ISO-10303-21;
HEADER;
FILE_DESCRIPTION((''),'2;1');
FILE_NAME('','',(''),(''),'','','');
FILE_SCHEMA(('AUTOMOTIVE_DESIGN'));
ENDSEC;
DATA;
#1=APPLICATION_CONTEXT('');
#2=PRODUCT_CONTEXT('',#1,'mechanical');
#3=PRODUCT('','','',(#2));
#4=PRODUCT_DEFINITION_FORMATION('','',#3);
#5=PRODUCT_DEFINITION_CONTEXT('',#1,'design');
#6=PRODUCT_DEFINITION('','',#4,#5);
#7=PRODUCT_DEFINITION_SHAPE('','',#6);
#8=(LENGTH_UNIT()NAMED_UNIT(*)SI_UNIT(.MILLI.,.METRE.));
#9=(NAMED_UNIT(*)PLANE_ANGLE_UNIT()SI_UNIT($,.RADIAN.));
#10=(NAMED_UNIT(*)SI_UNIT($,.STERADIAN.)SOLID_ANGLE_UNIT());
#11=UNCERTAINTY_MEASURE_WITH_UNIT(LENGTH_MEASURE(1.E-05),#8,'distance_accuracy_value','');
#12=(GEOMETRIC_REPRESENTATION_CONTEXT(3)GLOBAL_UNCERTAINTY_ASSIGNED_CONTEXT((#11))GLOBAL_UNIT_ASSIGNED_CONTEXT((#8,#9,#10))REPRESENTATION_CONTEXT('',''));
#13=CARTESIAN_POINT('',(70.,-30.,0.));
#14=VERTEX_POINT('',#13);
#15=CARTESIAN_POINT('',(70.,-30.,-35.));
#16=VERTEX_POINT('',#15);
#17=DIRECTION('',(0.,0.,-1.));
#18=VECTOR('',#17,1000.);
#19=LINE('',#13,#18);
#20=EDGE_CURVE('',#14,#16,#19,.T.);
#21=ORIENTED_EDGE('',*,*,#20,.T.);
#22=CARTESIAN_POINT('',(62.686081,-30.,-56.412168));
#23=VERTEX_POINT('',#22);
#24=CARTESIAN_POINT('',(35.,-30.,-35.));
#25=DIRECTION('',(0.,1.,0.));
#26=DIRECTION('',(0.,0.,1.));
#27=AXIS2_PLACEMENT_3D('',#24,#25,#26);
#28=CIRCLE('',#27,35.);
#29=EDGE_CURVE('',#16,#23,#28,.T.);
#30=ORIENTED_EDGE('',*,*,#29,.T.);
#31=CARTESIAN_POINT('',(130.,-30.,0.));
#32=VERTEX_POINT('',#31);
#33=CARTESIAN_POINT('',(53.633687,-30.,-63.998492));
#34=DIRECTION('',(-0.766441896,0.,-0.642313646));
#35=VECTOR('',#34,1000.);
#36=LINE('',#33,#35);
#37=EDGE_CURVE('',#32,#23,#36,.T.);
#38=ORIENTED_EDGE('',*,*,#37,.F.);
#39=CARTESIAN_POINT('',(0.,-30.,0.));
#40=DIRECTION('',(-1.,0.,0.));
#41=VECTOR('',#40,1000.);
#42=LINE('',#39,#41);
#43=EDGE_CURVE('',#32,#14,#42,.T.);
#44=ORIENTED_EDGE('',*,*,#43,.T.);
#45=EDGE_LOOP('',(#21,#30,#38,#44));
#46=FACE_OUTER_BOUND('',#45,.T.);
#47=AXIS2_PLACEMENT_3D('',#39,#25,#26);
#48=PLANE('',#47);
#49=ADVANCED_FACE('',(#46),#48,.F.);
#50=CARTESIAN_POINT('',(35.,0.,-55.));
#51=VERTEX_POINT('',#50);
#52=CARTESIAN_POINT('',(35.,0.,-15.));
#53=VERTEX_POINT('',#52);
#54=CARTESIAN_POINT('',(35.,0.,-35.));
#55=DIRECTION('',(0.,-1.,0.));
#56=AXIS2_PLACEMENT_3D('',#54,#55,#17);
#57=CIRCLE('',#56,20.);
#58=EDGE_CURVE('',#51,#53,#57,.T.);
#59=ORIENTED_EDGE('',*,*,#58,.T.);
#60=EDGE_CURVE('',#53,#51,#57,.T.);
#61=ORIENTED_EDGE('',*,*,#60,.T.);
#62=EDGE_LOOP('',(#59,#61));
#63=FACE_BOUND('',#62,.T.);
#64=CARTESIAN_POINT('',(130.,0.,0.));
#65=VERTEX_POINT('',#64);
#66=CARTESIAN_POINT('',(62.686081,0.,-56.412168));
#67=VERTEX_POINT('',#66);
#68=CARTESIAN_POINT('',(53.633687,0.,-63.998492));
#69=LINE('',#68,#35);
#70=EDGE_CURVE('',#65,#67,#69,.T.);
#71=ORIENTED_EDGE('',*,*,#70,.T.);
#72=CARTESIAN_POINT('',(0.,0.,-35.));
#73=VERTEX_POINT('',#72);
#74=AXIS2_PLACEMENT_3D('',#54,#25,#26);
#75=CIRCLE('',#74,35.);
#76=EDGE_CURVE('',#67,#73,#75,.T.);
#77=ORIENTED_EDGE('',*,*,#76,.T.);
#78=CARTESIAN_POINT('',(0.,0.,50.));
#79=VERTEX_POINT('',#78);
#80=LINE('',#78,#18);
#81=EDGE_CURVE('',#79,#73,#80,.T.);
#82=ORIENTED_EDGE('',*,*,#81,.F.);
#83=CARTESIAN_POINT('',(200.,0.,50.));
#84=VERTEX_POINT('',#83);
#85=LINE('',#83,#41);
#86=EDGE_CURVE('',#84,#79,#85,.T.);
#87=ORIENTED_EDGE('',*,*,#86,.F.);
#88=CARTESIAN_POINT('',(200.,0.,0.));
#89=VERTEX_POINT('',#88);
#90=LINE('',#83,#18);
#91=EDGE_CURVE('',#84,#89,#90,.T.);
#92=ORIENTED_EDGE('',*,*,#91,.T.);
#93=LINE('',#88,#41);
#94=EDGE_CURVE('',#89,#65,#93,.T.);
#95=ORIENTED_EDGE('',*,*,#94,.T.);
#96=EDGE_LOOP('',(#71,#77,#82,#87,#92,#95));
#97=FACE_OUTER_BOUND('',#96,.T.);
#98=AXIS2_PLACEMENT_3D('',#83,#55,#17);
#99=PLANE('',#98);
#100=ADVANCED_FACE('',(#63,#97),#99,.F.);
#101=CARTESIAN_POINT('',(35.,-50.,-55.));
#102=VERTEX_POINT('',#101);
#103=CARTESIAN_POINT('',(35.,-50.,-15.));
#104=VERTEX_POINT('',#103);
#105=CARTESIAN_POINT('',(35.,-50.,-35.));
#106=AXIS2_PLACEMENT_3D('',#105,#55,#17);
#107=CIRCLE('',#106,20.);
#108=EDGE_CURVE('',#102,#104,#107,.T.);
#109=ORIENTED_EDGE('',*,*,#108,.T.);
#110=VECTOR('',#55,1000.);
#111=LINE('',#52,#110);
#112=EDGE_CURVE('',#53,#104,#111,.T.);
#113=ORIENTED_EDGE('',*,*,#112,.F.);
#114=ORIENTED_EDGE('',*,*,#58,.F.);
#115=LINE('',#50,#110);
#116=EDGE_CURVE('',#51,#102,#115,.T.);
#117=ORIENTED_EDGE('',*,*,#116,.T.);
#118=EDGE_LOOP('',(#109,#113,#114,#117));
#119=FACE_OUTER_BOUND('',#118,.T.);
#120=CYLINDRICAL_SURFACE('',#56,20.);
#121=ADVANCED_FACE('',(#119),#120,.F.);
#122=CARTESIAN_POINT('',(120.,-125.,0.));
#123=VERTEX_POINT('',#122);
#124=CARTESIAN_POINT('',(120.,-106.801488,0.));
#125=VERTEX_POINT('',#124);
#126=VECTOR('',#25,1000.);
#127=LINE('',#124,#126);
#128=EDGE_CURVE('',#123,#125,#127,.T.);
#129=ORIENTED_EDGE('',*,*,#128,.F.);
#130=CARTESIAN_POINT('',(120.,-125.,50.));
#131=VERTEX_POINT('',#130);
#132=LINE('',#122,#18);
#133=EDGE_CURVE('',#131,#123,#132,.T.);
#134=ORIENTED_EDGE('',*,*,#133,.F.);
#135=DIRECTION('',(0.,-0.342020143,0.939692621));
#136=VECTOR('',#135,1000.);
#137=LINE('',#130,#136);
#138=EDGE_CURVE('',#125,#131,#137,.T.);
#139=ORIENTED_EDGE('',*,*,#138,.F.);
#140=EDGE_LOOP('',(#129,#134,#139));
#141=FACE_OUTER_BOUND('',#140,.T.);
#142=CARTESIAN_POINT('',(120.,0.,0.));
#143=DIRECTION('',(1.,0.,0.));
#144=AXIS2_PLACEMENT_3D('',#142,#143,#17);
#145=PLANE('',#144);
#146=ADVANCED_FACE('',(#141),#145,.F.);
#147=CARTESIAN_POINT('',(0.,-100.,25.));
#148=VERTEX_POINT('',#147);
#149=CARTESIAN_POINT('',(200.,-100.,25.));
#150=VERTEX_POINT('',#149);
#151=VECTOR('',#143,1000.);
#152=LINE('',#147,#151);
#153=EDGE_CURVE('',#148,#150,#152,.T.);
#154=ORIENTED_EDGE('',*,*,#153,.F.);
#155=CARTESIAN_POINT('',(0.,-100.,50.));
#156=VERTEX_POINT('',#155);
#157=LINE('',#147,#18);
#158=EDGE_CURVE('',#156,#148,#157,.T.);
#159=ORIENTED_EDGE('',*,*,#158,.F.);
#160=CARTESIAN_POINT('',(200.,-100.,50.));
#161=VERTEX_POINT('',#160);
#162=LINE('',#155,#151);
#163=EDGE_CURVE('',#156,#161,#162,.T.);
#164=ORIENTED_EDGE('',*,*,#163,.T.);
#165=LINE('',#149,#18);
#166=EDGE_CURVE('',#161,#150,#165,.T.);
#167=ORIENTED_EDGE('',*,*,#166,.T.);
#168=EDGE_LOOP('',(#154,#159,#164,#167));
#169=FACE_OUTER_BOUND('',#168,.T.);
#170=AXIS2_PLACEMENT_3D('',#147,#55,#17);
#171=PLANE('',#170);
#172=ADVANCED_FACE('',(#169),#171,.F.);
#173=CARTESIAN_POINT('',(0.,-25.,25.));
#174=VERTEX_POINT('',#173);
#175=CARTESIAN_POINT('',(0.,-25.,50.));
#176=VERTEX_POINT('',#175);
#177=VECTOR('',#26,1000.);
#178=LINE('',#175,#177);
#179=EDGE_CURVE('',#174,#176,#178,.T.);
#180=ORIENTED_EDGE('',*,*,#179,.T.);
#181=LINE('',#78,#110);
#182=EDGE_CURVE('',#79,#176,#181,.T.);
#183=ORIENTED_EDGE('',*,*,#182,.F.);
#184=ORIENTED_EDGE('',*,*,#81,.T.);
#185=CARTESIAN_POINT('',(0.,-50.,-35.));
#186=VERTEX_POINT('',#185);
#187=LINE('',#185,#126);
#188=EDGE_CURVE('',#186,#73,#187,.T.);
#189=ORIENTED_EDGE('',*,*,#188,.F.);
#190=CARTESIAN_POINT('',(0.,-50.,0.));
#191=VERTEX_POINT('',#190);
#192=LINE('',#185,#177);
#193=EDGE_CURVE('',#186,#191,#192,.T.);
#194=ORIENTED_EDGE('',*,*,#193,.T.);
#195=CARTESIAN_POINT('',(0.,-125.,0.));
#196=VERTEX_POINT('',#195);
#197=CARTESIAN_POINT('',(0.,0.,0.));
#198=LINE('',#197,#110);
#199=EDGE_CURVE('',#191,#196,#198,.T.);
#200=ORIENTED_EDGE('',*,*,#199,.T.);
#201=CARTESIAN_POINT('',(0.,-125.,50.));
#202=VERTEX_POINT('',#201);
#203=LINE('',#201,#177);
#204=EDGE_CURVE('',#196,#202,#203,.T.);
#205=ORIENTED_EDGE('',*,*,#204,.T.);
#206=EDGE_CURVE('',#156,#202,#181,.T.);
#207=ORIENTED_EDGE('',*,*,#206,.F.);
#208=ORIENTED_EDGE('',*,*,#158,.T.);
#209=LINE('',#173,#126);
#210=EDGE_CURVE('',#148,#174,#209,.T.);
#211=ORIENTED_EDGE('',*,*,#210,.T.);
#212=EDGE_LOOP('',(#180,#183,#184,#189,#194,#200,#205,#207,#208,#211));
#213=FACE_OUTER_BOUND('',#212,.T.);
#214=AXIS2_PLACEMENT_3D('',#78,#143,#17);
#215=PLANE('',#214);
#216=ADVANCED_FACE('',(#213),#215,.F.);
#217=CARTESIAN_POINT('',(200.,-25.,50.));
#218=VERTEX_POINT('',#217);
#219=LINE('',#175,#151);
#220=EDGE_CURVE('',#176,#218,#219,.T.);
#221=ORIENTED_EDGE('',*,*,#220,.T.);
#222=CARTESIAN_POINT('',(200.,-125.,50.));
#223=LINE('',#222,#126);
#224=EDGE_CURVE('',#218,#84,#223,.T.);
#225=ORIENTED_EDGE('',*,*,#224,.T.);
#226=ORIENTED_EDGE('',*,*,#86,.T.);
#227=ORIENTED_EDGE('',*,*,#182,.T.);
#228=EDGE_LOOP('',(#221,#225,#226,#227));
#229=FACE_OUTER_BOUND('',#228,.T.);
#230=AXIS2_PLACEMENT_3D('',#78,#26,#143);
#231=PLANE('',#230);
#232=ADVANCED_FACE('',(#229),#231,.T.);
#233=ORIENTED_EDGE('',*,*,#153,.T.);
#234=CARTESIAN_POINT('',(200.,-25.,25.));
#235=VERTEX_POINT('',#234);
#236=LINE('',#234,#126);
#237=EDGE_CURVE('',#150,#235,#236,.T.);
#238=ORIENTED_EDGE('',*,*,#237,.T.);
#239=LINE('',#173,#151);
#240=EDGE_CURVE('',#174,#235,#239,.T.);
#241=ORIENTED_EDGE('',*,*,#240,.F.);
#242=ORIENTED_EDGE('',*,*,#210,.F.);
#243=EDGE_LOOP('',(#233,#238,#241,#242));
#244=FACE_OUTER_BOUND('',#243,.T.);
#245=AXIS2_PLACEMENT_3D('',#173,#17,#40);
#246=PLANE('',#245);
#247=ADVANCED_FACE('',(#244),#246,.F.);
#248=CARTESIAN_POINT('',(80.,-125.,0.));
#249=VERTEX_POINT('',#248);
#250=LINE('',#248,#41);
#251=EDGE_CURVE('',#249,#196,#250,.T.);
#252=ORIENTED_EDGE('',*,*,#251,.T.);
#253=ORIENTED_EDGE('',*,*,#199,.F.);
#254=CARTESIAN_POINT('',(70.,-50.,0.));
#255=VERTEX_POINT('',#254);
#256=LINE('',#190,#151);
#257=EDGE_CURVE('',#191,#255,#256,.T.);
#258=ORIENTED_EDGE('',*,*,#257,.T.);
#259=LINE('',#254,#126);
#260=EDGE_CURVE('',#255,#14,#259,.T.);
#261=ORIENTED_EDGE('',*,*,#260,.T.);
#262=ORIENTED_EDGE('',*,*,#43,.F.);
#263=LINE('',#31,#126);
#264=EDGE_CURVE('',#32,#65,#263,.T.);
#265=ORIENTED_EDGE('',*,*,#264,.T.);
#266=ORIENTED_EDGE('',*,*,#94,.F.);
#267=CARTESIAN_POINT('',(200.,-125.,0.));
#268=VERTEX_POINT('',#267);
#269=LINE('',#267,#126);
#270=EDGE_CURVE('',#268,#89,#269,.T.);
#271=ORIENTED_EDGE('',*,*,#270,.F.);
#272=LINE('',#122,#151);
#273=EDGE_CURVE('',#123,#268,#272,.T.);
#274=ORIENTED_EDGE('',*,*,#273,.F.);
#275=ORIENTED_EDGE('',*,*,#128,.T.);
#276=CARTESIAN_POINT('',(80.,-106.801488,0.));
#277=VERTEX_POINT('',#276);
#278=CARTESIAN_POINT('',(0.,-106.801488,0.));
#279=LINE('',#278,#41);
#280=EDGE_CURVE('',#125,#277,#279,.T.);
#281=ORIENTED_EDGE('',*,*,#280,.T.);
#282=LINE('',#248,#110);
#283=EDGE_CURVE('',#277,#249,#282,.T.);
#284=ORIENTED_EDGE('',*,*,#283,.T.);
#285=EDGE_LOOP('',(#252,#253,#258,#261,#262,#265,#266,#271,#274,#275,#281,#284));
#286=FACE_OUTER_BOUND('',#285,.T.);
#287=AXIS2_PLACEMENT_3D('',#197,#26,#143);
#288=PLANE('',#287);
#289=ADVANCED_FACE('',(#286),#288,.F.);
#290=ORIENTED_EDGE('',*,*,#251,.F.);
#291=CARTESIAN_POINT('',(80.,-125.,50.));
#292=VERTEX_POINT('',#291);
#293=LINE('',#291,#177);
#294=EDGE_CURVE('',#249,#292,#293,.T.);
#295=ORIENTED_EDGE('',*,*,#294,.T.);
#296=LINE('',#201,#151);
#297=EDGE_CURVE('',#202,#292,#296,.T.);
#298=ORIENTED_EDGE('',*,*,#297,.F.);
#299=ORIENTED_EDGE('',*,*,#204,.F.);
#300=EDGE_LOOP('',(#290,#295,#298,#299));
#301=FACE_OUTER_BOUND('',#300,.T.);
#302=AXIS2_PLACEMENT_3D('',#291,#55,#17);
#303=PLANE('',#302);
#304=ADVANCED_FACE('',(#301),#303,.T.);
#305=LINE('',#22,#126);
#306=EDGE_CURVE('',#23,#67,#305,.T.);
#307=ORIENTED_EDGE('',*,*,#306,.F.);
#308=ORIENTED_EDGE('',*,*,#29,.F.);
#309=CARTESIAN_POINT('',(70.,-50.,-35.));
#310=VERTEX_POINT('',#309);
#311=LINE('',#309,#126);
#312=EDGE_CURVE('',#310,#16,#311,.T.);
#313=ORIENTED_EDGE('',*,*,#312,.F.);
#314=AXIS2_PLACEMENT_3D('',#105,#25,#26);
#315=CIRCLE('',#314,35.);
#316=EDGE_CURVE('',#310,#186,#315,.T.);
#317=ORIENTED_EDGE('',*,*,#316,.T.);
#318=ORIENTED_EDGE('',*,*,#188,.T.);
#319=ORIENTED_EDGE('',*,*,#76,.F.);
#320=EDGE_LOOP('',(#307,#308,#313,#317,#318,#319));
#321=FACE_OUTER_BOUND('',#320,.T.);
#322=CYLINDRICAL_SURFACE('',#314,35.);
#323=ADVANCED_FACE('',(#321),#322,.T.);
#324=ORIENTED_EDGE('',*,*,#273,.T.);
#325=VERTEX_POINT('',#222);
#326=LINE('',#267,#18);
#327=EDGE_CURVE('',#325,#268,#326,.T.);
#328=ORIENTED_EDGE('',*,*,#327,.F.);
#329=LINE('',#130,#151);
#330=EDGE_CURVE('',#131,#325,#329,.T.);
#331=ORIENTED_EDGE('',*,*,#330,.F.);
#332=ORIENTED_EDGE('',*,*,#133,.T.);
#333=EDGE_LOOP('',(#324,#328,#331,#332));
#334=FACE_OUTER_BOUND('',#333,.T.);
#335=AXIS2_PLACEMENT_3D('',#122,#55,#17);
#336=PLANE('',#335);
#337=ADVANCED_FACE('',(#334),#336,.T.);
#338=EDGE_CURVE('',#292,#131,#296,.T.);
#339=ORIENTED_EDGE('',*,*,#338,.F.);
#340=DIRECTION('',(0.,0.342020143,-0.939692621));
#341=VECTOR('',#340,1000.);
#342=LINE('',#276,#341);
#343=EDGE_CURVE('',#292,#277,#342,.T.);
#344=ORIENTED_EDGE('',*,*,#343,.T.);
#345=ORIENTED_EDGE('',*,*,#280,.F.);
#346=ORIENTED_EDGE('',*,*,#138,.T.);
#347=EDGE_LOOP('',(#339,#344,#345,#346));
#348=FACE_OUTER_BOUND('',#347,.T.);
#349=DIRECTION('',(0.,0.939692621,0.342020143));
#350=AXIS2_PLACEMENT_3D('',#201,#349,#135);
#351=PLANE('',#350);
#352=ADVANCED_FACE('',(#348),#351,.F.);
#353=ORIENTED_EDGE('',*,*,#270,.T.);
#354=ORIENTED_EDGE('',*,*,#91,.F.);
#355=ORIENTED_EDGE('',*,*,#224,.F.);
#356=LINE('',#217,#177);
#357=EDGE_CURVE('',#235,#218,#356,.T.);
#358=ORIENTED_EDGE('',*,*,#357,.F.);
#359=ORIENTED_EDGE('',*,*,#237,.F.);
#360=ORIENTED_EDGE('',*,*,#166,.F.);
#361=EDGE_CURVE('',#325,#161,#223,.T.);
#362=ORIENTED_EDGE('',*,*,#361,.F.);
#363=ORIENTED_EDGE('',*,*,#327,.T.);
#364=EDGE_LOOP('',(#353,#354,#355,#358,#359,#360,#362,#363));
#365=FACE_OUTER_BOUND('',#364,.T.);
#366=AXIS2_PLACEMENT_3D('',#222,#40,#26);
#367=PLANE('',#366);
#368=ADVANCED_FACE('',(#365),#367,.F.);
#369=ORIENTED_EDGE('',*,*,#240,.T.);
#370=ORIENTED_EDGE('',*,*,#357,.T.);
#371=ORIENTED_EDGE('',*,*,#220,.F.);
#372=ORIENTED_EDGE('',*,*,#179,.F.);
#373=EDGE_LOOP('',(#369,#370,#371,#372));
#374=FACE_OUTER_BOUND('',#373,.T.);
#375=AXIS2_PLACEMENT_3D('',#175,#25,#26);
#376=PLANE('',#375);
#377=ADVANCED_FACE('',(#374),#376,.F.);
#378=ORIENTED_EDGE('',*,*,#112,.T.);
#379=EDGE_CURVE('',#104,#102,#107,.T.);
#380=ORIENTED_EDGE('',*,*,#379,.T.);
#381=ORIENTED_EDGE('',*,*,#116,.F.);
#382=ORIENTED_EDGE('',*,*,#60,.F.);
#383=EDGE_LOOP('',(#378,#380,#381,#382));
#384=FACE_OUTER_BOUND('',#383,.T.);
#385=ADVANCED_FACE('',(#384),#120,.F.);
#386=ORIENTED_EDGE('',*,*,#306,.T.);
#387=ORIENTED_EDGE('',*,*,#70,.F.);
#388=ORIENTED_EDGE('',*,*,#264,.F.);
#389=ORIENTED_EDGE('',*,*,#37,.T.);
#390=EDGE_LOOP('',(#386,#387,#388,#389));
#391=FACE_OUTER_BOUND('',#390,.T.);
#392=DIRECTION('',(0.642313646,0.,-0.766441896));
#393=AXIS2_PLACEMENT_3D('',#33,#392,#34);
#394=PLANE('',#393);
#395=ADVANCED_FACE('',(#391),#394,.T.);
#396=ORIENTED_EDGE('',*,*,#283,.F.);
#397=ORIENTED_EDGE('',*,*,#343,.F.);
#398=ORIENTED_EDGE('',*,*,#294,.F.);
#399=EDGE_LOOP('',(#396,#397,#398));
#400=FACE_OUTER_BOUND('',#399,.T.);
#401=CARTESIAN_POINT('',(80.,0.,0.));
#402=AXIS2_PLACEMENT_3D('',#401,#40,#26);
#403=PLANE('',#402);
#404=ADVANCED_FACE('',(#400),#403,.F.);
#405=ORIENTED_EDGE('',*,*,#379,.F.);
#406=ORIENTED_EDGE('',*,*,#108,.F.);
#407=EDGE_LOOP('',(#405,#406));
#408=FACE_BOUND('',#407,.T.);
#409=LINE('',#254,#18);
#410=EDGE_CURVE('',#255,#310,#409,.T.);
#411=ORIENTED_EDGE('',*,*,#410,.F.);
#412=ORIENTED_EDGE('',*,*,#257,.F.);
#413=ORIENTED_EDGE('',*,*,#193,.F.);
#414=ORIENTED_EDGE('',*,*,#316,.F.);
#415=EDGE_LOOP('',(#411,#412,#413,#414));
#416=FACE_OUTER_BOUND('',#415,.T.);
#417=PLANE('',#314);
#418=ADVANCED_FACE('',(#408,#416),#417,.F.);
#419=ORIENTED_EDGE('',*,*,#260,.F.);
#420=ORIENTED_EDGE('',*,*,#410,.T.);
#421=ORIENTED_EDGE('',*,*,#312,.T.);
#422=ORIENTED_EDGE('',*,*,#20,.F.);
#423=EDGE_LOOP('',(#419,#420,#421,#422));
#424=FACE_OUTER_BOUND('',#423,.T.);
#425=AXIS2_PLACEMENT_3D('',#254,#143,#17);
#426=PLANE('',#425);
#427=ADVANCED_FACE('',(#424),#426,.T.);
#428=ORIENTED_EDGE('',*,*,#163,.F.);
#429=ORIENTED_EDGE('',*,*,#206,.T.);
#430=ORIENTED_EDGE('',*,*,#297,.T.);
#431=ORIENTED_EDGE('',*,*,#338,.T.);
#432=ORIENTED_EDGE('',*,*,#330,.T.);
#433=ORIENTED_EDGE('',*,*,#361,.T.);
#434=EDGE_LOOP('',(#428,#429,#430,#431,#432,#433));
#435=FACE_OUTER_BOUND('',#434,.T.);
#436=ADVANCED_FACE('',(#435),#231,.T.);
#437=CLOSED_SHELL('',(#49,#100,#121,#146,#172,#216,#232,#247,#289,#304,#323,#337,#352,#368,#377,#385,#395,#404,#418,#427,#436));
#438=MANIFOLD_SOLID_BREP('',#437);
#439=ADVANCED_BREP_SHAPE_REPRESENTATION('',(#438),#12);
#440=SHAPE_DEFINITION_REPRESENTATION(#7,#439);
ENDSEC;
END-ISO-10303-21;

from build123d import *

# Parameters (mm, degrees)
BASE_BLOCK_SKETCH_W   = 200
BASE_BLOCK_SKETCH_H   = 125
BASE_BLOCK_DEPTH      = 50
UPPER_BLOCK_DEPTH     = 50
LUG_BOSS_DEPTH        = 30
LUG_BORE_SKETCH_R     = 20
LUG_BORE_DEPTH        = 50
CHANNEL_CUT_DEPTH     = 200
CORNER_TRIM_CUT_DEPTH = 200
TAPER_FILL_1_DEPTH    = 80
TAPER_FILL_2_DEPTH    = 80


with BuildPart() as part:
    # Base Block Sketch → Base Block (new body)
    with BuildSketch(Plane.XY):
        with Locations((100, -62.5)):
            Rectangle(BASE_BLOCK_SKETCH_W, BASE_BLOCK_SKETCH_H)
    extrude(amount=BASE_BLOCK_DEPTH)

    # Upper Block Sketch → Upper Block (add)
    with BuildSketch(Plane(origin=(0, 0, 0), x_dir=(1, 0, 0), z_dir=(0, 1, 0))):
        with BuildLine():
            Line((0, 0), (70, 0))
            Line((70, 0), (70, 35))
            ThreePointArc((70, 35), (35, 70), (0, 35))
            Line((0, 35), (0, 0))
        make_face()
    extrude(amount=-UPPER_BLOCK_DEPTH)

    # Lug Sketch → Lug Boss (add)
    with BuildSketch(Plane(origin=(0, 0, 0), x_dir=(1, 0, 0), z_dir=(0, 1, 0))):
        with BuildLine():
            Line((70, 0), (130, 0))
            Line((130, 0), (62.686080753, 56.412167861))
            ThreePointArc((62.686080753, 56.412167861), (68.121087138, 46.31342507), (70, 35))
            Line((70, 35), (70, 0))
        make_face()
    extrude(amount=-LUG_BOSS_DEPTH)

    # Lug Bore Sketch → Lug Bore (cut)
    with BuildSketch(Plane.XZ.offset(50)):
        with Locations(Location((35, -35, 0), (0, 0, 270))):
            Circle(LUG_BORE_SKETCH_R)
    extrude(amount=-LUG_BORE_DEPTH, mode=Mode.SUBTRACT)

    # Channel Sketch → Channel Cut (cut)
    with BuildSketch(Plane(origin=(200, 0, 0), x_dir=(0, 0, -1), z_dir=(1, 0, 0))):
        Polygon((-50, -62.5), (-50, -25), (-25, -25), (-25, -100), (-50, -100), align=None)
    extrude(amount=-CHANNEL_CUT_DEPTH, mode=Mode.SUBTRACT)

    # Corner Trim Sketch → Corner Trim Cut (cut)
    with BuildSketch(Plane(origin=(200, 0, 0), x_dir=(0, 0, -1), z_dir=(1, 0, 0))):
        Polygon((-50, -125), (0.050929029, -106.782951636), (0, -125), align=None)
    extrude(amount=-CORNER_TRIM_CUT_DEPTH, mode=Mode.SUBTRACT)

    # Taper Fill 1 Sketch → Taper Fill 1 (add)
    with BuildSketch(Plane(origin=(200, 0, 0), x_dir=(0, 0, -1), z_dir=(1, 0, 0))):
        Polygon((-50, -125), (0, -106.801488287), (0, -125), align=None)
    extrude(amount=-TAPER_FILL_1_DEPTH)

    # Taper Fill 2 Sketch → Taper Fill 2 (add)
    with BuildSketch(Plane.ZY):
        Polygon((0, -106.801488287), (50, -125), (0, -125), align=None)
    extrude(amount=-TAPER_FILL_2_DEPTH)


solid = part.part
